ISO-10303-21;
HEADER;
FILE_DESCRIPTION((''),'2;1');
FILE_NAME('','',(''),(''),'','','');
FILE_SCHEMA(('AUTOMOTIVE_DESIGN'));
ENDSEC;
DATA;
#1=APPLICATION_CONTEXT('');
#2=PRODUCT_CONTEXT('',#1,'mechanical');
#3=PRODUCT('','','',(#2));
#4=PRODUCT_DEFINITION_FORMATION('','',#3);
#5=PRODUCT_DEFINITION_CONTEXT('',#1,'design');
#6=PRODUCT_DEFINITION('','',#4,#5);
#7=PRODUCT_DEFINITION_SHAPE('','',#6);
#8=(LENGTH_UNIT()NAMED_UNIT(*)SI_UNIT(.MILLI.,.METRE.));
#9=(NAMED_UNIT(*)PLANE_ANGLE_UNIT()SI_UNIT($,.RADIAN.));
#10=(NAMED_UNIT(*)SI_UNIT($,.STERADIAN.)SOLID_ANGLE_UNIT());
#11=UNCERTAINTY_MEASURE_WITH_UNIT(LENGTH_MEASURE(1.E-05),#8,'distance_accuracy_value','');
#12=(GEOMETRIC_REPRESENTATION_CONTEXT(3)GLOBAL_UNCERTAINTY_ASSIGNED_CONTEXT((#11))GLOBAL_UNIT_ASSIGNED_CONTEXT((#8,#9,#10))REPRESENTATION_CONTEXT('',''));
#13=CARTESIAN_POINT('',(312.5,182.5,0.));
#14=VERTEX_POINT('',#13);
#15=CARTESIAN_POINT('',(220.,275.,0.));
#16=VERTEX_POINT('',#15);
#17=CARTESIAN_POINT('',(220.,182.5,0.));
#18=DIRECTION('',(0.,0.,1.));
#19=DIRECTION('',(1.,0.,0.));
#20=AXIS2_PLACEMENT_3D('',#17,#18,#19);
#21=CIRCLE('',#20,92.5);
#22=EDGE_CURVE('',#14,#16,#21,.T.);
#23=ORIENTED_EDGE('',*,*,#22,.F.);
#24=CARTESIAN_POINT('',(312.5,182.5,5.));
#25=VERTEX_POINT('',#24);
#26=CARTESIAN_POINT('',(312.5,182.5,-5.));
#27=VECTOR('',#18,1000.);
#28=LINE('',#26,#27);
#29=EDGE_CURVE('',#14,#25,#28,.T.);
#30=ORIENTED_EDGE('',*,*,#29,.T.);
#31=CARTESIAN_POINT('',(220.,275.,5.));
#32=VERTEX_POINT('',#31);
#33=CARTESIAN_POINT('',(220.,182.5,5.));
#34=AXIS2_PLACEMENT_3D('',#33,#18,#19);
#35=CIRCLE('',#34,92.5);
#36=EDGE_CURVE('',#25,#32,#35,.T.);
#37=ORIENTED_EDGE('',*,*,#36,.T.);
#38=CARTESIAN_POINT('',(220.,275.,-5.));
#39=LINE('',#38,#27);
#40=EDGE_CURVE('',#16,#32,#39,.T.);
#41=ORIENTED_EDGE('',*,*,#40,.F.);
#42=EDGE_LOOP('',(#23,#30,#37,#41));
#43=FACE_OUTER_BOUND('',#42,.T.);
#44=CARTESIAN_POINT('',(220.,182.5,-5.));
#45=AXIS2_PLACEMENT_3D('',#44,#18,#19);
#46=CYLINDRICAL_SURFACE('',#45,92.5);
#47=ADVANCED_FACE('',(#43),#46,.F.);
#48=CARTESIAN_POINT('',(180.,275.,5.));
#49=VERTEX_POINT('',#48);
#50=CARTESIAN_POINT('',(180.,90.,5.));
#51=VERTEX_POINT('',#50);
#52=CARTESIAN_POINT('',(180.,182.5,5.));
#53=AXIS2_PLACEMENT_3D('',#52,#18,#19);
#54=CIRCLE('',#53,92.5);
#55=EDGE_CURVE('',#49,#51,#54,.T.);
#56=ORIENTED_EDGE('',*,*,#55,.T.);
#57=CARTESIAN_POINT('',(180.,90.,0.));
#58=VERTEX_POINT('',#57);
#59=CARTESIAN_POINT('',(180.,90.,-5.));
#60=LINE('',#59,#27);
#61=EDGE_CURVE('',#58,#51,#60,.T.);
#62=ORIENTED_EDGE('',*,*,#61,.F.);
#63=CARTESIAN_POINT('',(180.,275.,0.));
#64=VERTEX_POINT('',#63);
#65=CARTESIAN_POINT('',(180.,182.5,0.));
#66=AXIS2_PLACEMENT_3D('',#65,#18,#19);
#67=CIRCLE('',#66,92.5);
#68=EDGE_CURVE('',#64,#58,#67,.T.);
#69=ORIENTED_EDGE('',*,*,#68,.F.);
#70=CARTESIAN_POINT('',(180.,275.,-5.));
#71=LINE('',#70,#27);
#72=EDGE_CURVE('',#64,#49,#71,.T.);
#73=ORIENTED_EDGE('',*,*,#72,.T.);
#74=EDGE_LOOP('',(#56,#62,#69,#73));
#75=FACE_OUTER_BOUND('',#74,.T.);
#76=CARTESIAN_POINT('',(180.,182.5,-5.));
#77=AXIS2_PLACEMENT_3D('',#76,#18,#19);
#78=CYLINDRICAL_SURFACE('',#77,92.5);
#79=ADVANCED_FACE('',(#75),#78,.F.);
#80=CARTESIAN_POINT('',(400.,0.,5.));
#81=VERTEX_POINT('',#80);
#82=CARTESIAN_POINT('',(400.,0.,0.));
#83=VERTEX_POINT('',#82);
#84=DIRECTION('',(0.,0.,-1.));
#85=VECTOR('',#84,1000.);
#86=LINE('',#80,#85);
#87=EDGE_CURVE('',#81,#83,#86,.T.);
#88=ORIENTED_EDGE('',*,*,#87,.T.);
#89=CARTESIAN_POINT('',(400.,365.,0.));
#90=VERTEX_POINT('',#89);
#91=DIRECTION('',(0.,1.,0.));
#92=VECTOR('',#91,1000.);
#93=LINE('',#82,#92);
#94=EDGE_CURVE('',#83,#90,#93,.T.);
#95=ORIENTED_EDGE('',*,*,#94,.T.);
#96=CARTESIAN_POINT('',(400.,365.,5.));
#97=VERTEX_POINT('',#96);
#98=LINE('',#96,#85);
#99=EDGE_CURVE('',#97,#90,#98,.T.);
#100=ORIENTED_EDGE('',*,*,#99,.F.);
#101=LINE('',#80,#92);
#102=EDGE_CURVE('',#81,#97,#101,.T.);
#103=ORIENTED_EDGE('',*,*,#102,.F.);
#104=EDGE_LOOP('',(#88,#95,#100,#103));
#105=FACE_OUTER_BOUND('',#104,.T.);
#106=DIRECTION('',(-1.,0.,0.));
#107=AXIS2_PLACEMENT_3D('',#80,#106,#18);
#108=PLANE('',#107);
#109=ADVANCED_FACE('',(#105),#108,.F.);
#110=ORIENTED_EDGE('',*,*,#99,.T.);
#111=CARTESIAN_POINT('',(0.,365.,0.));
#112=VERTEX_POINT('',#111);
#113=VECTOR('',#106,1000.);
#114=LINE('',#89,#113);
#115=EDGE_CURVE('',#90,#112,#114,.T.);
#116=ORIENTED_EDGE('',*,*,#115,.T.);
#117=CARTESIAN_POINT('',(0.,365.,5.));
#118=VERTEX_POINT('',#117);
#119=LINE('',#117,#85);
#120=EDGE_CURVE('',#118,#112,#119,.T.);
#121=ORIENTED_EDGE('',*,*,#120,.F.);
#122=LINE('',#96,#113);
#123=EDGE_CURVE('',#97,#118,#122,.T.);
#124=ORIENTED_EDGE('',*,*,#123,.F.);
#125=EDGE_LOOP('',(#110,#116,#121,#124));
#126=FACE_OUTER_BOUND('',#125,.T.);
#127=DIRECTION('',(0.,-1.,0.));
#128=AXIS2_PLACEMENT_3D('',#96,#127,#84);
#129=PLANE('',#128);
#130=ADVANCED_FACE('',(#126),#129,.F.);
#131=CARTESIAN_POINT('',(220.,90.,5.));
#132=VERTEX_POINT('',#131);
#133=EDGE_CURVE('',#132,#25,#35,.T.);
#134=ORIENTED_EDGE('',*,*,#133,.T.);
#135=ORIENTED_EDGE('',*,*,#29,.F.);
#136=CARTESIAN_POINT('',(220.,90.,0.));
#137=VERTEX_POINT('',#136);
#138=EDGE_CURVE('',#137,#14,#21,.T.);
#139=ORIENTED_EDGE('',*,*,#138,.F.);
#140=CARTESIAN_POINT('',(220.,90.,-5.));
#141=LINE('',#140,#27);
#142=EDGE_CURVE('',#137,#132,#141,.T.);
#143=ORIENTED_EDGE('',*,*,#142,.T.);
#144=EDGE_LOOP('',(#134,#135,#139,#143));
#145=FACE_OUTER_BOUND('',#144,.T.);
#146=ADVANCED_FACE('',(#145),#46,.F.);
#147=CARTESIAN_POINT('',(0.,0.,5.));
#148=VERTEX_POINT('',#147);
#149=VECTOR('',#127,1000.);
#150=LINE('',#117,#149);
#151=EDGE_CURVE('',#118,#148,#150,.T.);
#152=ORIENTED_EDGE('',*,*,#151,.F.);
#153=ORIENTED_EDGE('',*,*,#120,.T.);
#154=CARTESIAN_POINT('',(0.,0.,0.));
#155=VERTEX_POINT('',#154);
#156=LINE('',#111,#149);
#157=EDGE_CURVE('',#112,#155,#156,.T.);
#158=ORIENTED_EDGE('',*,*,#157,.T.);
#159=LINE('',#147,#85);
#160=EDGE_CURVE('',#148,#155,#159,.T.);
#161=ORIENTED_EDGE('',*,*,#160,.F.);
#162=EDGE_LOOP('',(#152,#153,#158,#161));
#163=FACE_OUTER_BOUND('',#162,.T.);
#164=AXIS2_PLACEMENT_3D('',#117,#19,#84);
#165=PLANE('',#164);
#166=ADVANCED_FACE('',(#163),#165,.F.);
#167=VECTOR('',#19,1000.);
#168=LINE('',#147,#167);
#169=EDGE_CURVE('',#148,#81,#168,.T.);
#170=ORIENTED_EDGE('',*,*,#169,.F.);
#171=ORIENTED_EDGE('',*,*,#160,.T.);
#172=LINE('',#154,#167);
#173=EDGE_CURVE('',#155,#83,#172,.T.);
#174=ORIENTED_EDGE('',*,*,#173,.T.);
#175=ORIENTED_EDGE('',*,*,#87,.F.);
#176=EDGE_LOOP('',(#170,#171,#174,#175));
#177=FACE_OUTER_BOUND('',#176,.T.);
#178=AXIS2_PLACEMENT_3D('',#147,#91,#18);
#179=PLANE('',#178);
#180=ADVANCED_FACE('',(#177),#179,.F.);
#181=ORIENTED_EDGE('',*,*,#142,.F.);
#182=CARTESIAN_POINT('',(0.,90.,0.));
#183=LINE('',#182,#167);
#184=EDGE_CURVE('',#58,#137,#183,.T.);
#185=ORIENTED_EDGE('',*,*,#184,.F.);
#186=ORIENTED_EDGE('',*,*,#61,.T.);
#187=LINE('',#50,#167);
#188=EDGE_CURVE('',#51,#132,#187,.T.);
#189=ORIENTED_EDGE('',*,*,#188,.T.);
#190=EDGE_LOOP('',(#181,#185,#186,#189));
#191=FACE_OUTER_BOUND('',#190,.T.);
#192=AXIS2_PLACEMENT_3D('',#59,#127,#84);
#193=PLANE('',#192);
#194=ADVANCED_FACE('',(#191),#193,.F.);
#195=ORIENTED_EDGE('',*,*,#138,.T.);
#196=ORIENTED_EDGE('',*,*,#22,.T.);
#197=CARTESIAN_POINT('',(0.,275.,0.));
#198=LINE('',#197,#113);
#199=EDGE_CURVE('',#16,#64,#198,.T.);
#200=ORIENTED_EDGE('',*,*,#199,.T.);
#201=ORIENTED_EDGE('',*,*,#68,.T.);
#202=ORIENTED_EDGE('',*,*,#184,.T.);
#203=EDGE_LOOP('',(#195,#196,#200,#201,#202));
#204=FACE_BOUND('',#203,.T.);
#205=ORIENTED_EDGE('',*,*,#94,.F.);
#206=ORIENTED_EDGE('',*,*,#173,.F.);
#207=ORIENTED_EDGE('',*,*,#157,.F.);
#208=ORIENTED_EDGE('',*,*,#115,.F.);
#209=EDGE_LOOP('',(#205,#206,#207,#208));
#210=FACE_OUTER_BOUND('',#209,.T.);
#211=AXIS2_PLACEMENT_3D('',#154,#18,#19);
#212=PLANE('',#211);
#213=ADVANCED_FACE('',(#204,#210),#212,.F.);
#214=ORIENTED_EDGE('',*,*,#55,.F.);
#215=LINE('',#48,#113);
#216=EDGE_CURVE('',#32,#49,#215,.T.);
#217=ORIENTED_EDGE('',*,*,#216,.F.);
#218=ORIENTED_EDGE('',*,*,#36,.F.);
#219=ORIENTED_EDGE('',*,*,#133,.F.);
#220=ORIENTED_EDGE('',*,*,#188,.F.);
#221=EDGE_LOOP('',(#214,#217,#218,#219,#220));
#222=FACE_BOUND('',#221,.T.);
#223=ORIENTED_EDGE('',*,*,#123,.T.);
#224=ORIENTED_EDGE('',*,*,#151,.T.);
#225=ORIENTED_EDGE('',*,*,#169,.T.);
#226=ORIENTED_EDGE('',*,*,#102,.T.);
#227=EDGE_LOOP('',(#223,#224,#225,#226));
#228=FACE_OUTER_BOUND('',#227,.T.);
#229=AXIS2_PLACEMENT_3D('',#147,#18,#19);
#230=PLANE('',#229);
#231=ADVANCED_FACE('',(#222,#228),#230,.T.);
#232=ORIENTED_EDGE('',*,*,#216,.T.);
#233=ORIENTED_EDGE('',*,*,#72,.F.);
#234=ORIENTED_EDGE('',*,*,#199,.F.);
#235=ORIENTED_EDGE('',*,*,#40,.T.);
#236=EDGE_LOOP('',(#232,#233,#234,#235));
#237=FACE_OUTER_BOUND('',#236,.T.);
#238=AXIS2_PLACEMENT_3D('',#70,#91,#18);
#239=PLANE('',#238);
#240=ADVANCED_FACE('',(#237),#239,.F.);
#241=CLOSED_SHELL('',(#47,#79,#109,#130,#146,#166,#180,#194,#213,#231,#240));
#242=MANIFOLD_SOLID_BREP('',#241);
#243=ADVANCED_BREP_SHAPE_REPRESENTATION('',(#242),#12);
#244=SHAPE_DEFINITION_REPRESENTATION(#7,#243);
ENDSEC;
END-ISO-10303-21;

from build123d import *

# Parameters (mm, degrees)
SKETCH_1_W          = 400
SKETCH_1_H          = 365
EXTRUDE_1_DEPTH     = 5
CUT_EXTRUDE_3_DEPTH = 10


with BuildPart() as part:
    # 草图1 → 凸台-拉伸1 (new body)
    with BuildSketch(Plane.XY):
        with Locations((200, 182.5)):
            Rectangle(SKETCH_1_W, SKETCH_1_H)
    extrude(amount=EXTRUDE_1_DEPTH)

    # 草图4 → 切除-拉伸3 (cut)
    with BuildSketch(Plane.XY.offset(5)):
        with BuildLine():
            Line((180, 275), (220, 275))
            ThreePointArc((220, 275), (312.5, 182.5), (220, 90))
            Line((220, 90), (180, 90))
            ThreePointArc((180, 90), (87.5, 182.5), (180, 275))
        make_face()
    extrude(amount=-CUT_EXTRUDE_3_DEPTH, mode=Mode.SUBTRACT)


solid = part.part
